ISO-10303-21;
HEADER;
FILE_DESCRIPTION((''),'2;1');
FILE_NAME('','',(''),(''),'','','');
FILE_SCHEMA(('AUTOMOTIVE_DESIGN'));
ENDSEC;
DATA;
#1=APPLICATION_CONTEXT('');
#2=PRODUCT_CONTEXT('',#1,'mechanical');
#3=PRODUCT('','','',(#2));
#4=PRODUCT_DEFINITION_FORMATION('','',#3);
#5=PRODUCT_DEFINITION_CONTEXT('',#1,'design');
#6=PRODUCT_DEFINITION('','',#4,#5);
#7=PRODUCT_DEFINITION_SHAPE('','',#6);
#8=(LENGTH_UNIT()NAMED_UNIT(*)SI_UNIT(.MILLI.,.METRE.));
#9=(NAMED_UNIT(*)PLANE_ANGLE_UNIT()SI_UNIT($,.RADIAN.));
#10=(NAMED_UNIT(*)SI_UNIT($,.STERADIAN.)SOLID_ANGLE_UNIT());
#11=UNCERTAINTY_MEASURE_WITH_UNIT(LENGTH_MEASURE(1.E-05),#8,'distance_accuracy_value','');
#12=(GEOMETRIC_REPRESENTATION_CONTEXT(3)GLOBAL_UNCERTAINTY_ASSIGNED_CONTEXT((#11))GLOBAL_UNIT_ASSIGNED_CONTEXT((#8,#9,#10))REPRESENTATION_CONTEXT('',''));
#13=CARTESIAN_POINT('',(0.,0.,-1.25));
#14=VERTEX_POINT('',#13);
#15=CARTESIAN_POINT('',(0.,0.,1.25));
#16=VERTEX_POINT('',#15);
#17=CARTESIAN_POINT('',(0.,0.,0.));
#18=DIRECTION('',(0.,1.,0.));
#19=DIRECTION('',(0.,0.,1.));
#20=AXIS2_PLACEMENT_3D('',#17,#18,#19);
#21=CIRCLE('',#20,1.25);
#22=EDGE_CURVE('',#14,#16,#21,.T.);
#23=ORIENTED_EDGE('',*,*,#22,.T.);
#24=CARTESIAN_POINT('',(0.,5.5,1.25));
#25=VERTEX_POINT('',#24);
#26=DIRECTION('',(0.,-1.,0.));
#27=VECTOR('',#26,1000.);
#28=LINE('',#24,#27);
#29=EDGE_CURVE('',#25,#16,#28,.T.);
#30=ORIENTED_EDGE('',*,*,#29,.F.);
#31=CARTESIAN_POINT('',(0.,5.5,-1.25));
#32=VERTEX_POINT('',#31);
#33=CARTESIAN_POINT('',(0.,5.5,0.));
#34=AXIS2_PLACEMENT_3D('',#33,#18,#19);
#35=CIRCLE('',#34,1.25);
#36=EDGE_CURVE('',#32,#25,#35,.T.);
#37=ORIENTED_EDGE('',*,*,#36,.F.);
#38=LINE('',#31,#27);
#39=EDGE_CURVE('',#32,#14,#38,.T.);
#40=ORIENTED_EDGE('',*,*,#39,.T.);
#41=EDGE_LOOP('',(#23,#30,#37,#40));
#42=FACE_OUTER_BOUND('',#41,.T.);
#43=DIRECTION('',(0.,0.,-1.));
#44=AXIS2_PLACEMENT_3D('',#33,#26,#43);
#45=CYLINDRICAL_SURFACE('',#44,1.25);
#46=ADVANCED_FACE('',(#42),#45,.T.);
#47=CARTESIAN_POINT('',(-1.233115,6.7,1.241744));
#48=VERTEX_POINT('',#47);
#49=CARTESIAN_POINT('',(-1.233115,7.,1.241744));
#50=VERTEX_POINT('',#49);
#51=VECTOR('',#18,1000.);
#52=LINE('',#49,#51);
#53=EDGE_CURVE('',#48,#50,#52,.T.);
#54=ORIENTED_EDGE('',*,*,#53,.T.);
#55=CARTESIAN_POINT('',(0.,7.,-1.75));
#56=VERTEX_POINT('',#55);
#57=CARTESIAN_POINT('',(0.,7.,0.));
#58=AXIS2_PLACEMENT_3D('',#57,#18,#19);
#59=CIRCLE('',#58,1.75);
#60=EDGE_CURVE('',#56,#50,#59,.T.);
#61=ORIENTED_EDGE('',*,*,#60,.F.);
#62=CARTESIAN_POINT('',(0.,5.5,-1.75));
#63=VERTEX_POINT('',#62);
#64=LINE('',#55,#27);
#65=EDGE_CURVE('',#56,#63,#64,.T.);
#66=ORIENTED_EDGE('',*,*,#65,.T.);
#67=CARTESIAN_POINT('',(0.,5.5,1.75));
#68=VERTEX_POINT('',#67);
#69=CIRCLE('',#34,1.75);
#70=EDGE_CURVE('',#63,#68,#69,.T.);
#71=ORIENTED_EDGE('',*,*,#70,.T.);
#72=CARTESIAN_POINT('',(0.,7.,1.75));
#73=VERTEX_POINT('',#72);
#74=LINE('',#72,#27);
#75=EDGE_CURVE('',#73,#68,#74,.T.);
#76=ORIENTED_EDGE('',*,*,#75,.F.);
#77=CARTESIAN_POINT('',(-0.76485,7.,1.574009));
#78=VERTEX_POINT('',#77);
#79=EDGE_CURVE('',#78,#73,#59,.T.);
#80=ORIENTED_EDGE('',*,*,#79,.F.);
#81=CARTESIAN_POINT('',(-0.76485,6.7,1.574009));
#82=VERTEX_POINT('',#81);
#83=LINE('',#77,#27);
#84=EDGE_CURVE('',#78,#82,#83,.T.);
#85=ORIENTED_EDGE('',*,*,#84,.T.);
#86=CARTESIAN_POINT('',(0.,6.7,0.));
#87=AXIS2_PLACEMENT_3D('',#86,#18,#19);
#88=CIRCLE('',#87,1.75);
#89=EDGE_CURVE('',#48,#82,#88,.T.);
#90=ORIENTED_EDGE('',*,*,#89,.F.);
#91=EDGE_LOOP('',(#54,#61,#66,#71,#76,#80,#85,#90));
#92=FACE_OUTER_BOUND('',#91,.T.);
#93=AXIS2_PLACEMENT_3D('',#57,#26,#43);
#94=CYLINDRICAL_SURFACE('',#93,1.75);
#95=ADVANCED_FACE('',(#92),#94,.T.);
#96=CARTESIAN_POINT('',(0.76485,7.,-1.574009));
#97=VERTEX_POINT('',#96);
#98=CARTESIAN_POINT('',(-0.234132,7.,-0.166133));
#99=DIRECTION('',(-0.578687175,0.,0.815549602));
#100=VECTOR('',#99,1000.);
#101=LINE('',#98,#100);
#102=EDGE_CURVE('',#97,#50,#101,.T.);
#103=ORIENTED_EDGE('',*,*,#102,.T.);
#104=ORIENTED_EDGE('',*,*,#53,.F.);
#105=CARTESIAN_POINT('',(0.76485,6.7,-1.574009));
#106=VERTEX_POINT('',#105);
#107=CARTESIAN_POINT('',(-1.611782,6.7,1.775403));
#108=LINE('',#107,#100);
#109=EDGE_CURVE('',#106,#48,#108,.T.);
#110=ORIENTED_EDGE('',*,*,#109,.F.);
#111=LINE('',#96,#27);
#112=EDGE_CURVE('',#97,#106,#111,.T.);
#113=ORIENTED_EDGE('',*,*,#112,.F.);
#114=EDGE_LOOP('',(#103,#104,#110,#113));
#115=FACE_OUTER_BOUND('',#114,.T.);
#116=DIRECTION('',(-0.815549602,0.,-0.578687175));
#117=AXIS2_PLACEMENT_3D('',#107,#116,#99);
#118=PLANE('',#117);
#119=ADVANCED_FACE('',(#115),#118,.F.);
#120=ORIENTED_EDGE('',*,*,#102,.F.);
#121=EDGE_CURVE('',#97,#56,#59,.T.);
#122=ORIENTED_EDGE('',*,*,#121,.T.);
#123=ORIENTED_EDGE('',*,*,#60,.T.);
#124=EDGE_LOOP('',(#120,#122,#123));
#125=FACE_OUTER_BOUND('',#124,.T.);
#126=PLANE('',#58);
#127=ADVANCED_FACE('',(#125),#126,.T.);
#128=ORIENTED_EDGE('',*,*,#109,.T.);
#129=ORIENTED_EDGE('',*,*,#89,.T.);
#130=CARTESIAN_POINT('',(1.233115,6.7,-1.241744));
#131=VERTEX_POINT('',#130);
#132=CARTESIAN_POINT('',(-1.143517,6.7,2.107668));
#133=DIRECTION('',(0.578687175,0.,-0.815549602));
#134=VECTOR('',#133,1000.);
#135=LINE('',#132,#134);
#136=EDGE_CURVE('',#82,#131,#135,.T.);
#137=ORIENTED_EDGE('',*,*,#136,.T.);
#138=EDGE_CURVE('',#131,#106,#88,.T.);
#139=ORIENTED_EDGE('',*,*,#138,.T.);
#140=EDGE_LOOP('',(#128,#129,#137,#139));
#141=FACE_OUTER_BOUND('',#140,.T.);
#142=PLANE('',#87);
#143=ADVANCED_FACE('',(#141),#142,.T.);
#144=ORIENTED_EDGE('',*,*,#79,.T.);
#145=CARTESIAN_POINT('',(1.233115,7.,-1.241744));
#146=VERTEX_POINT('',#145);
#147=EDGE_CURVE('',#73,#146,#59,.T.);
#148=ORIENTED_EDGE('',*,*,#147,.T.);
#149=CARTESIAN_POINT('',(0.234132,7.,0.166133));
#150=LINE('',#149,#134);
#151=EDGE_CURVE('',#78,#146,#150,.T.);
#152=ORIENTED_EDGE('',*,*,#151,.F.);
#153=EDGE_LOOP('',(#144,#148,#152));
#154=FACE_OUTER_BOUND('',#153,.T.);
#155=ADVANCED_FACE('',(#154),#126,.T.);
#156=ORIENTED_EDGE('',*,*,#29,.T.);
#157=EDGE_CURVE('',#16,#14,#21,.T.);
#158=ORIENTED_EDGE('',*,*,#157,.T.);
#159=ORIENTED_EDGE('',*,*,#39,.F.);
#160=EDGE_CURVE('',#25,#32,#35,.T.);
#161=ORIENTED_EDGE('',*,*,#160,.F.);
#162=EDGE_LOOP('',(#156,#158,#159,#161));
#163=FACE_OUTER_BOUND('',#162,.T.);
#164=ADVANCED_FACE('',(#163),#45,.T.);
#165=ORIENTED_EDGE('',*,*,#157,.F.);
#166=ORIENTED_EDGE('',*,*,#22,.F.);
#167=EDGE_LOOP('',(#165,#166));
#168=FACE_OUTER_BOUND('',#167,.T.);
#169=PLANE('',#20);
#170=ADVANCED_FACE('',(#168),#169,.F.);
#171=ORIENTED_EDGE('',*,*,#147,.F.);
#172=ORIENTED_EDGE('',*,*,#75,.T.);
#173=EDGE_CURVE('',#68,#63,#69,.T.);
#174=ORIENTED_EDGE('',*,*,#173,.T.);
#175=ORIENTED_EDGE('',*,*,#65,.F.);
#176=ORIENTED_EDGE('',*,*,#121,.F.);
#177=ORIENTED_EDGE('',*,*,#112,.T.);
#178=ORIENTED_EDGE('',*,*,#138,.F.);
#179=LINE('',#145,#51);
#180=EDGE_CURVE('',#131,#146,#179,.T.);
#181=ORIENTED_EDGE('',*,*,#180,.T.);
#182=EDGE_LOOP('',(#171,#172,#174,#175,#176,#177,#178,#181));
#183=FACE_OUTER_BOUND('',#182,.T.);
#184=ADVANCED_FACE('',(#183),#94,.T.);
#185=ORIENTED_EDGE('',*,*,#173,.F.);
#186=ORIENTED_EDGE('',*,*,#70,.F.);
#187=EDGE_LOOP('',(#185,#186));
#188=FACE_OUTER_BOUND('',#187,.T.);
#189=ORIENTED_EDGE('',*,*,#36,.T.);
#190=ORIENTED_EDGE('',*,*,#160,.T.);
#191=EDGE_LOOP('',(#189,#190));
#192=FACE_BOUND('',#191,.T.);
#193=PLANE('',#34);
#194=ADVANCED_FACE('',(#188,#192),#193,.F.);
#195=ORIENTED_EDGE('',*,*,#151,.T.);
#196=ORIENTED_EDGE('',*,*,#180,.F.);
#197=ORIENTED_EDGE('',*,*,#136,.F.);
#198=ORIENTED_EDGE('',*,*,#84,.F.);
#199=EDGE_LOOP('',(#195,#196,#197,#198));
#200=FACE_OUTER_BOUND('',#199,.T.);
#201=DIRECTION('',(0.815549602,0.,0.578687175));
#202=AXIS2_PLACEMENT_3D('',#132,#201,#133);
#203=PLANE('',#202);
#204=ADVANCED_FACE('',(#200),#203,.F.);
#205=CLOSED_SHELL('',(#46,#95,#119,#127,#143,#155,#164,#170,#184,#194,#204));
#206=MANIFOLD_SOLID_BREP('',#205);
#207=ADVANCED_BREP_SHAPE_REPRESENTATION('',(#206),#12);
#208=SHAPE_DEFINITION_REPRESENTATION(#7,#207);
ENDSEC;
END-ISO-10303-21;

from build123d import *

# Parameters (mm, degrees)
SKETCH1_R           = 1.25
BOSS_EXTRUDE1_DEPTH = 5.5
SKETCH2_R           = 1.75
BOSS_EXTRUDE2_DEPTH = 1.5
CUT_EXTRUDE1_DEPTH  = 0.3


with BuildPart() as part:
    # Sketch1 → Boss-Extrude1 (new body)
    with BuildSketch(Plane(origin=(0, 0, 0), x_dir=(1, 0, 0), z_dir=(0, 1, 0))):
        with Locations(Location((0, 0, 0), (0, 0, 270))):
            Circle(SKETCH1_R)
    extrude(amount=BOSS_EXTRUDE1_DEPTH)

    # Sketch2 → Boss-Extrude2 (add)
    with BuildSketch(Plane(origin=(0, 5.5, 0), x_dir=(1, 0, 0), z_dir=(0, 1, 0))):
        with Locations(Location((0, 0, 0), (0, 0, 270))):
            Circle(SKETCH2_R)
    extrude(amount=BOSS_EXTRUDE2_DEPTH)

    # Sketch3 → Cut-Extrude1 (cut)
    with BuildSketch(Plane(origin=(0, 7, 0), x_dir=(1, 0, 0), z_dir=(0, 1, 0))):
        Polygon((-1.611781927, -1.775402925), (1.143517474, 2.10766798), (1.611781927, 1.775402925), (-1.143517474, -2.10766798), align=None)
    extrude(amount=-CUT_EXTRUDE1_DEPTH, mode=Mode.SUBTRACT)


solid = part.part
